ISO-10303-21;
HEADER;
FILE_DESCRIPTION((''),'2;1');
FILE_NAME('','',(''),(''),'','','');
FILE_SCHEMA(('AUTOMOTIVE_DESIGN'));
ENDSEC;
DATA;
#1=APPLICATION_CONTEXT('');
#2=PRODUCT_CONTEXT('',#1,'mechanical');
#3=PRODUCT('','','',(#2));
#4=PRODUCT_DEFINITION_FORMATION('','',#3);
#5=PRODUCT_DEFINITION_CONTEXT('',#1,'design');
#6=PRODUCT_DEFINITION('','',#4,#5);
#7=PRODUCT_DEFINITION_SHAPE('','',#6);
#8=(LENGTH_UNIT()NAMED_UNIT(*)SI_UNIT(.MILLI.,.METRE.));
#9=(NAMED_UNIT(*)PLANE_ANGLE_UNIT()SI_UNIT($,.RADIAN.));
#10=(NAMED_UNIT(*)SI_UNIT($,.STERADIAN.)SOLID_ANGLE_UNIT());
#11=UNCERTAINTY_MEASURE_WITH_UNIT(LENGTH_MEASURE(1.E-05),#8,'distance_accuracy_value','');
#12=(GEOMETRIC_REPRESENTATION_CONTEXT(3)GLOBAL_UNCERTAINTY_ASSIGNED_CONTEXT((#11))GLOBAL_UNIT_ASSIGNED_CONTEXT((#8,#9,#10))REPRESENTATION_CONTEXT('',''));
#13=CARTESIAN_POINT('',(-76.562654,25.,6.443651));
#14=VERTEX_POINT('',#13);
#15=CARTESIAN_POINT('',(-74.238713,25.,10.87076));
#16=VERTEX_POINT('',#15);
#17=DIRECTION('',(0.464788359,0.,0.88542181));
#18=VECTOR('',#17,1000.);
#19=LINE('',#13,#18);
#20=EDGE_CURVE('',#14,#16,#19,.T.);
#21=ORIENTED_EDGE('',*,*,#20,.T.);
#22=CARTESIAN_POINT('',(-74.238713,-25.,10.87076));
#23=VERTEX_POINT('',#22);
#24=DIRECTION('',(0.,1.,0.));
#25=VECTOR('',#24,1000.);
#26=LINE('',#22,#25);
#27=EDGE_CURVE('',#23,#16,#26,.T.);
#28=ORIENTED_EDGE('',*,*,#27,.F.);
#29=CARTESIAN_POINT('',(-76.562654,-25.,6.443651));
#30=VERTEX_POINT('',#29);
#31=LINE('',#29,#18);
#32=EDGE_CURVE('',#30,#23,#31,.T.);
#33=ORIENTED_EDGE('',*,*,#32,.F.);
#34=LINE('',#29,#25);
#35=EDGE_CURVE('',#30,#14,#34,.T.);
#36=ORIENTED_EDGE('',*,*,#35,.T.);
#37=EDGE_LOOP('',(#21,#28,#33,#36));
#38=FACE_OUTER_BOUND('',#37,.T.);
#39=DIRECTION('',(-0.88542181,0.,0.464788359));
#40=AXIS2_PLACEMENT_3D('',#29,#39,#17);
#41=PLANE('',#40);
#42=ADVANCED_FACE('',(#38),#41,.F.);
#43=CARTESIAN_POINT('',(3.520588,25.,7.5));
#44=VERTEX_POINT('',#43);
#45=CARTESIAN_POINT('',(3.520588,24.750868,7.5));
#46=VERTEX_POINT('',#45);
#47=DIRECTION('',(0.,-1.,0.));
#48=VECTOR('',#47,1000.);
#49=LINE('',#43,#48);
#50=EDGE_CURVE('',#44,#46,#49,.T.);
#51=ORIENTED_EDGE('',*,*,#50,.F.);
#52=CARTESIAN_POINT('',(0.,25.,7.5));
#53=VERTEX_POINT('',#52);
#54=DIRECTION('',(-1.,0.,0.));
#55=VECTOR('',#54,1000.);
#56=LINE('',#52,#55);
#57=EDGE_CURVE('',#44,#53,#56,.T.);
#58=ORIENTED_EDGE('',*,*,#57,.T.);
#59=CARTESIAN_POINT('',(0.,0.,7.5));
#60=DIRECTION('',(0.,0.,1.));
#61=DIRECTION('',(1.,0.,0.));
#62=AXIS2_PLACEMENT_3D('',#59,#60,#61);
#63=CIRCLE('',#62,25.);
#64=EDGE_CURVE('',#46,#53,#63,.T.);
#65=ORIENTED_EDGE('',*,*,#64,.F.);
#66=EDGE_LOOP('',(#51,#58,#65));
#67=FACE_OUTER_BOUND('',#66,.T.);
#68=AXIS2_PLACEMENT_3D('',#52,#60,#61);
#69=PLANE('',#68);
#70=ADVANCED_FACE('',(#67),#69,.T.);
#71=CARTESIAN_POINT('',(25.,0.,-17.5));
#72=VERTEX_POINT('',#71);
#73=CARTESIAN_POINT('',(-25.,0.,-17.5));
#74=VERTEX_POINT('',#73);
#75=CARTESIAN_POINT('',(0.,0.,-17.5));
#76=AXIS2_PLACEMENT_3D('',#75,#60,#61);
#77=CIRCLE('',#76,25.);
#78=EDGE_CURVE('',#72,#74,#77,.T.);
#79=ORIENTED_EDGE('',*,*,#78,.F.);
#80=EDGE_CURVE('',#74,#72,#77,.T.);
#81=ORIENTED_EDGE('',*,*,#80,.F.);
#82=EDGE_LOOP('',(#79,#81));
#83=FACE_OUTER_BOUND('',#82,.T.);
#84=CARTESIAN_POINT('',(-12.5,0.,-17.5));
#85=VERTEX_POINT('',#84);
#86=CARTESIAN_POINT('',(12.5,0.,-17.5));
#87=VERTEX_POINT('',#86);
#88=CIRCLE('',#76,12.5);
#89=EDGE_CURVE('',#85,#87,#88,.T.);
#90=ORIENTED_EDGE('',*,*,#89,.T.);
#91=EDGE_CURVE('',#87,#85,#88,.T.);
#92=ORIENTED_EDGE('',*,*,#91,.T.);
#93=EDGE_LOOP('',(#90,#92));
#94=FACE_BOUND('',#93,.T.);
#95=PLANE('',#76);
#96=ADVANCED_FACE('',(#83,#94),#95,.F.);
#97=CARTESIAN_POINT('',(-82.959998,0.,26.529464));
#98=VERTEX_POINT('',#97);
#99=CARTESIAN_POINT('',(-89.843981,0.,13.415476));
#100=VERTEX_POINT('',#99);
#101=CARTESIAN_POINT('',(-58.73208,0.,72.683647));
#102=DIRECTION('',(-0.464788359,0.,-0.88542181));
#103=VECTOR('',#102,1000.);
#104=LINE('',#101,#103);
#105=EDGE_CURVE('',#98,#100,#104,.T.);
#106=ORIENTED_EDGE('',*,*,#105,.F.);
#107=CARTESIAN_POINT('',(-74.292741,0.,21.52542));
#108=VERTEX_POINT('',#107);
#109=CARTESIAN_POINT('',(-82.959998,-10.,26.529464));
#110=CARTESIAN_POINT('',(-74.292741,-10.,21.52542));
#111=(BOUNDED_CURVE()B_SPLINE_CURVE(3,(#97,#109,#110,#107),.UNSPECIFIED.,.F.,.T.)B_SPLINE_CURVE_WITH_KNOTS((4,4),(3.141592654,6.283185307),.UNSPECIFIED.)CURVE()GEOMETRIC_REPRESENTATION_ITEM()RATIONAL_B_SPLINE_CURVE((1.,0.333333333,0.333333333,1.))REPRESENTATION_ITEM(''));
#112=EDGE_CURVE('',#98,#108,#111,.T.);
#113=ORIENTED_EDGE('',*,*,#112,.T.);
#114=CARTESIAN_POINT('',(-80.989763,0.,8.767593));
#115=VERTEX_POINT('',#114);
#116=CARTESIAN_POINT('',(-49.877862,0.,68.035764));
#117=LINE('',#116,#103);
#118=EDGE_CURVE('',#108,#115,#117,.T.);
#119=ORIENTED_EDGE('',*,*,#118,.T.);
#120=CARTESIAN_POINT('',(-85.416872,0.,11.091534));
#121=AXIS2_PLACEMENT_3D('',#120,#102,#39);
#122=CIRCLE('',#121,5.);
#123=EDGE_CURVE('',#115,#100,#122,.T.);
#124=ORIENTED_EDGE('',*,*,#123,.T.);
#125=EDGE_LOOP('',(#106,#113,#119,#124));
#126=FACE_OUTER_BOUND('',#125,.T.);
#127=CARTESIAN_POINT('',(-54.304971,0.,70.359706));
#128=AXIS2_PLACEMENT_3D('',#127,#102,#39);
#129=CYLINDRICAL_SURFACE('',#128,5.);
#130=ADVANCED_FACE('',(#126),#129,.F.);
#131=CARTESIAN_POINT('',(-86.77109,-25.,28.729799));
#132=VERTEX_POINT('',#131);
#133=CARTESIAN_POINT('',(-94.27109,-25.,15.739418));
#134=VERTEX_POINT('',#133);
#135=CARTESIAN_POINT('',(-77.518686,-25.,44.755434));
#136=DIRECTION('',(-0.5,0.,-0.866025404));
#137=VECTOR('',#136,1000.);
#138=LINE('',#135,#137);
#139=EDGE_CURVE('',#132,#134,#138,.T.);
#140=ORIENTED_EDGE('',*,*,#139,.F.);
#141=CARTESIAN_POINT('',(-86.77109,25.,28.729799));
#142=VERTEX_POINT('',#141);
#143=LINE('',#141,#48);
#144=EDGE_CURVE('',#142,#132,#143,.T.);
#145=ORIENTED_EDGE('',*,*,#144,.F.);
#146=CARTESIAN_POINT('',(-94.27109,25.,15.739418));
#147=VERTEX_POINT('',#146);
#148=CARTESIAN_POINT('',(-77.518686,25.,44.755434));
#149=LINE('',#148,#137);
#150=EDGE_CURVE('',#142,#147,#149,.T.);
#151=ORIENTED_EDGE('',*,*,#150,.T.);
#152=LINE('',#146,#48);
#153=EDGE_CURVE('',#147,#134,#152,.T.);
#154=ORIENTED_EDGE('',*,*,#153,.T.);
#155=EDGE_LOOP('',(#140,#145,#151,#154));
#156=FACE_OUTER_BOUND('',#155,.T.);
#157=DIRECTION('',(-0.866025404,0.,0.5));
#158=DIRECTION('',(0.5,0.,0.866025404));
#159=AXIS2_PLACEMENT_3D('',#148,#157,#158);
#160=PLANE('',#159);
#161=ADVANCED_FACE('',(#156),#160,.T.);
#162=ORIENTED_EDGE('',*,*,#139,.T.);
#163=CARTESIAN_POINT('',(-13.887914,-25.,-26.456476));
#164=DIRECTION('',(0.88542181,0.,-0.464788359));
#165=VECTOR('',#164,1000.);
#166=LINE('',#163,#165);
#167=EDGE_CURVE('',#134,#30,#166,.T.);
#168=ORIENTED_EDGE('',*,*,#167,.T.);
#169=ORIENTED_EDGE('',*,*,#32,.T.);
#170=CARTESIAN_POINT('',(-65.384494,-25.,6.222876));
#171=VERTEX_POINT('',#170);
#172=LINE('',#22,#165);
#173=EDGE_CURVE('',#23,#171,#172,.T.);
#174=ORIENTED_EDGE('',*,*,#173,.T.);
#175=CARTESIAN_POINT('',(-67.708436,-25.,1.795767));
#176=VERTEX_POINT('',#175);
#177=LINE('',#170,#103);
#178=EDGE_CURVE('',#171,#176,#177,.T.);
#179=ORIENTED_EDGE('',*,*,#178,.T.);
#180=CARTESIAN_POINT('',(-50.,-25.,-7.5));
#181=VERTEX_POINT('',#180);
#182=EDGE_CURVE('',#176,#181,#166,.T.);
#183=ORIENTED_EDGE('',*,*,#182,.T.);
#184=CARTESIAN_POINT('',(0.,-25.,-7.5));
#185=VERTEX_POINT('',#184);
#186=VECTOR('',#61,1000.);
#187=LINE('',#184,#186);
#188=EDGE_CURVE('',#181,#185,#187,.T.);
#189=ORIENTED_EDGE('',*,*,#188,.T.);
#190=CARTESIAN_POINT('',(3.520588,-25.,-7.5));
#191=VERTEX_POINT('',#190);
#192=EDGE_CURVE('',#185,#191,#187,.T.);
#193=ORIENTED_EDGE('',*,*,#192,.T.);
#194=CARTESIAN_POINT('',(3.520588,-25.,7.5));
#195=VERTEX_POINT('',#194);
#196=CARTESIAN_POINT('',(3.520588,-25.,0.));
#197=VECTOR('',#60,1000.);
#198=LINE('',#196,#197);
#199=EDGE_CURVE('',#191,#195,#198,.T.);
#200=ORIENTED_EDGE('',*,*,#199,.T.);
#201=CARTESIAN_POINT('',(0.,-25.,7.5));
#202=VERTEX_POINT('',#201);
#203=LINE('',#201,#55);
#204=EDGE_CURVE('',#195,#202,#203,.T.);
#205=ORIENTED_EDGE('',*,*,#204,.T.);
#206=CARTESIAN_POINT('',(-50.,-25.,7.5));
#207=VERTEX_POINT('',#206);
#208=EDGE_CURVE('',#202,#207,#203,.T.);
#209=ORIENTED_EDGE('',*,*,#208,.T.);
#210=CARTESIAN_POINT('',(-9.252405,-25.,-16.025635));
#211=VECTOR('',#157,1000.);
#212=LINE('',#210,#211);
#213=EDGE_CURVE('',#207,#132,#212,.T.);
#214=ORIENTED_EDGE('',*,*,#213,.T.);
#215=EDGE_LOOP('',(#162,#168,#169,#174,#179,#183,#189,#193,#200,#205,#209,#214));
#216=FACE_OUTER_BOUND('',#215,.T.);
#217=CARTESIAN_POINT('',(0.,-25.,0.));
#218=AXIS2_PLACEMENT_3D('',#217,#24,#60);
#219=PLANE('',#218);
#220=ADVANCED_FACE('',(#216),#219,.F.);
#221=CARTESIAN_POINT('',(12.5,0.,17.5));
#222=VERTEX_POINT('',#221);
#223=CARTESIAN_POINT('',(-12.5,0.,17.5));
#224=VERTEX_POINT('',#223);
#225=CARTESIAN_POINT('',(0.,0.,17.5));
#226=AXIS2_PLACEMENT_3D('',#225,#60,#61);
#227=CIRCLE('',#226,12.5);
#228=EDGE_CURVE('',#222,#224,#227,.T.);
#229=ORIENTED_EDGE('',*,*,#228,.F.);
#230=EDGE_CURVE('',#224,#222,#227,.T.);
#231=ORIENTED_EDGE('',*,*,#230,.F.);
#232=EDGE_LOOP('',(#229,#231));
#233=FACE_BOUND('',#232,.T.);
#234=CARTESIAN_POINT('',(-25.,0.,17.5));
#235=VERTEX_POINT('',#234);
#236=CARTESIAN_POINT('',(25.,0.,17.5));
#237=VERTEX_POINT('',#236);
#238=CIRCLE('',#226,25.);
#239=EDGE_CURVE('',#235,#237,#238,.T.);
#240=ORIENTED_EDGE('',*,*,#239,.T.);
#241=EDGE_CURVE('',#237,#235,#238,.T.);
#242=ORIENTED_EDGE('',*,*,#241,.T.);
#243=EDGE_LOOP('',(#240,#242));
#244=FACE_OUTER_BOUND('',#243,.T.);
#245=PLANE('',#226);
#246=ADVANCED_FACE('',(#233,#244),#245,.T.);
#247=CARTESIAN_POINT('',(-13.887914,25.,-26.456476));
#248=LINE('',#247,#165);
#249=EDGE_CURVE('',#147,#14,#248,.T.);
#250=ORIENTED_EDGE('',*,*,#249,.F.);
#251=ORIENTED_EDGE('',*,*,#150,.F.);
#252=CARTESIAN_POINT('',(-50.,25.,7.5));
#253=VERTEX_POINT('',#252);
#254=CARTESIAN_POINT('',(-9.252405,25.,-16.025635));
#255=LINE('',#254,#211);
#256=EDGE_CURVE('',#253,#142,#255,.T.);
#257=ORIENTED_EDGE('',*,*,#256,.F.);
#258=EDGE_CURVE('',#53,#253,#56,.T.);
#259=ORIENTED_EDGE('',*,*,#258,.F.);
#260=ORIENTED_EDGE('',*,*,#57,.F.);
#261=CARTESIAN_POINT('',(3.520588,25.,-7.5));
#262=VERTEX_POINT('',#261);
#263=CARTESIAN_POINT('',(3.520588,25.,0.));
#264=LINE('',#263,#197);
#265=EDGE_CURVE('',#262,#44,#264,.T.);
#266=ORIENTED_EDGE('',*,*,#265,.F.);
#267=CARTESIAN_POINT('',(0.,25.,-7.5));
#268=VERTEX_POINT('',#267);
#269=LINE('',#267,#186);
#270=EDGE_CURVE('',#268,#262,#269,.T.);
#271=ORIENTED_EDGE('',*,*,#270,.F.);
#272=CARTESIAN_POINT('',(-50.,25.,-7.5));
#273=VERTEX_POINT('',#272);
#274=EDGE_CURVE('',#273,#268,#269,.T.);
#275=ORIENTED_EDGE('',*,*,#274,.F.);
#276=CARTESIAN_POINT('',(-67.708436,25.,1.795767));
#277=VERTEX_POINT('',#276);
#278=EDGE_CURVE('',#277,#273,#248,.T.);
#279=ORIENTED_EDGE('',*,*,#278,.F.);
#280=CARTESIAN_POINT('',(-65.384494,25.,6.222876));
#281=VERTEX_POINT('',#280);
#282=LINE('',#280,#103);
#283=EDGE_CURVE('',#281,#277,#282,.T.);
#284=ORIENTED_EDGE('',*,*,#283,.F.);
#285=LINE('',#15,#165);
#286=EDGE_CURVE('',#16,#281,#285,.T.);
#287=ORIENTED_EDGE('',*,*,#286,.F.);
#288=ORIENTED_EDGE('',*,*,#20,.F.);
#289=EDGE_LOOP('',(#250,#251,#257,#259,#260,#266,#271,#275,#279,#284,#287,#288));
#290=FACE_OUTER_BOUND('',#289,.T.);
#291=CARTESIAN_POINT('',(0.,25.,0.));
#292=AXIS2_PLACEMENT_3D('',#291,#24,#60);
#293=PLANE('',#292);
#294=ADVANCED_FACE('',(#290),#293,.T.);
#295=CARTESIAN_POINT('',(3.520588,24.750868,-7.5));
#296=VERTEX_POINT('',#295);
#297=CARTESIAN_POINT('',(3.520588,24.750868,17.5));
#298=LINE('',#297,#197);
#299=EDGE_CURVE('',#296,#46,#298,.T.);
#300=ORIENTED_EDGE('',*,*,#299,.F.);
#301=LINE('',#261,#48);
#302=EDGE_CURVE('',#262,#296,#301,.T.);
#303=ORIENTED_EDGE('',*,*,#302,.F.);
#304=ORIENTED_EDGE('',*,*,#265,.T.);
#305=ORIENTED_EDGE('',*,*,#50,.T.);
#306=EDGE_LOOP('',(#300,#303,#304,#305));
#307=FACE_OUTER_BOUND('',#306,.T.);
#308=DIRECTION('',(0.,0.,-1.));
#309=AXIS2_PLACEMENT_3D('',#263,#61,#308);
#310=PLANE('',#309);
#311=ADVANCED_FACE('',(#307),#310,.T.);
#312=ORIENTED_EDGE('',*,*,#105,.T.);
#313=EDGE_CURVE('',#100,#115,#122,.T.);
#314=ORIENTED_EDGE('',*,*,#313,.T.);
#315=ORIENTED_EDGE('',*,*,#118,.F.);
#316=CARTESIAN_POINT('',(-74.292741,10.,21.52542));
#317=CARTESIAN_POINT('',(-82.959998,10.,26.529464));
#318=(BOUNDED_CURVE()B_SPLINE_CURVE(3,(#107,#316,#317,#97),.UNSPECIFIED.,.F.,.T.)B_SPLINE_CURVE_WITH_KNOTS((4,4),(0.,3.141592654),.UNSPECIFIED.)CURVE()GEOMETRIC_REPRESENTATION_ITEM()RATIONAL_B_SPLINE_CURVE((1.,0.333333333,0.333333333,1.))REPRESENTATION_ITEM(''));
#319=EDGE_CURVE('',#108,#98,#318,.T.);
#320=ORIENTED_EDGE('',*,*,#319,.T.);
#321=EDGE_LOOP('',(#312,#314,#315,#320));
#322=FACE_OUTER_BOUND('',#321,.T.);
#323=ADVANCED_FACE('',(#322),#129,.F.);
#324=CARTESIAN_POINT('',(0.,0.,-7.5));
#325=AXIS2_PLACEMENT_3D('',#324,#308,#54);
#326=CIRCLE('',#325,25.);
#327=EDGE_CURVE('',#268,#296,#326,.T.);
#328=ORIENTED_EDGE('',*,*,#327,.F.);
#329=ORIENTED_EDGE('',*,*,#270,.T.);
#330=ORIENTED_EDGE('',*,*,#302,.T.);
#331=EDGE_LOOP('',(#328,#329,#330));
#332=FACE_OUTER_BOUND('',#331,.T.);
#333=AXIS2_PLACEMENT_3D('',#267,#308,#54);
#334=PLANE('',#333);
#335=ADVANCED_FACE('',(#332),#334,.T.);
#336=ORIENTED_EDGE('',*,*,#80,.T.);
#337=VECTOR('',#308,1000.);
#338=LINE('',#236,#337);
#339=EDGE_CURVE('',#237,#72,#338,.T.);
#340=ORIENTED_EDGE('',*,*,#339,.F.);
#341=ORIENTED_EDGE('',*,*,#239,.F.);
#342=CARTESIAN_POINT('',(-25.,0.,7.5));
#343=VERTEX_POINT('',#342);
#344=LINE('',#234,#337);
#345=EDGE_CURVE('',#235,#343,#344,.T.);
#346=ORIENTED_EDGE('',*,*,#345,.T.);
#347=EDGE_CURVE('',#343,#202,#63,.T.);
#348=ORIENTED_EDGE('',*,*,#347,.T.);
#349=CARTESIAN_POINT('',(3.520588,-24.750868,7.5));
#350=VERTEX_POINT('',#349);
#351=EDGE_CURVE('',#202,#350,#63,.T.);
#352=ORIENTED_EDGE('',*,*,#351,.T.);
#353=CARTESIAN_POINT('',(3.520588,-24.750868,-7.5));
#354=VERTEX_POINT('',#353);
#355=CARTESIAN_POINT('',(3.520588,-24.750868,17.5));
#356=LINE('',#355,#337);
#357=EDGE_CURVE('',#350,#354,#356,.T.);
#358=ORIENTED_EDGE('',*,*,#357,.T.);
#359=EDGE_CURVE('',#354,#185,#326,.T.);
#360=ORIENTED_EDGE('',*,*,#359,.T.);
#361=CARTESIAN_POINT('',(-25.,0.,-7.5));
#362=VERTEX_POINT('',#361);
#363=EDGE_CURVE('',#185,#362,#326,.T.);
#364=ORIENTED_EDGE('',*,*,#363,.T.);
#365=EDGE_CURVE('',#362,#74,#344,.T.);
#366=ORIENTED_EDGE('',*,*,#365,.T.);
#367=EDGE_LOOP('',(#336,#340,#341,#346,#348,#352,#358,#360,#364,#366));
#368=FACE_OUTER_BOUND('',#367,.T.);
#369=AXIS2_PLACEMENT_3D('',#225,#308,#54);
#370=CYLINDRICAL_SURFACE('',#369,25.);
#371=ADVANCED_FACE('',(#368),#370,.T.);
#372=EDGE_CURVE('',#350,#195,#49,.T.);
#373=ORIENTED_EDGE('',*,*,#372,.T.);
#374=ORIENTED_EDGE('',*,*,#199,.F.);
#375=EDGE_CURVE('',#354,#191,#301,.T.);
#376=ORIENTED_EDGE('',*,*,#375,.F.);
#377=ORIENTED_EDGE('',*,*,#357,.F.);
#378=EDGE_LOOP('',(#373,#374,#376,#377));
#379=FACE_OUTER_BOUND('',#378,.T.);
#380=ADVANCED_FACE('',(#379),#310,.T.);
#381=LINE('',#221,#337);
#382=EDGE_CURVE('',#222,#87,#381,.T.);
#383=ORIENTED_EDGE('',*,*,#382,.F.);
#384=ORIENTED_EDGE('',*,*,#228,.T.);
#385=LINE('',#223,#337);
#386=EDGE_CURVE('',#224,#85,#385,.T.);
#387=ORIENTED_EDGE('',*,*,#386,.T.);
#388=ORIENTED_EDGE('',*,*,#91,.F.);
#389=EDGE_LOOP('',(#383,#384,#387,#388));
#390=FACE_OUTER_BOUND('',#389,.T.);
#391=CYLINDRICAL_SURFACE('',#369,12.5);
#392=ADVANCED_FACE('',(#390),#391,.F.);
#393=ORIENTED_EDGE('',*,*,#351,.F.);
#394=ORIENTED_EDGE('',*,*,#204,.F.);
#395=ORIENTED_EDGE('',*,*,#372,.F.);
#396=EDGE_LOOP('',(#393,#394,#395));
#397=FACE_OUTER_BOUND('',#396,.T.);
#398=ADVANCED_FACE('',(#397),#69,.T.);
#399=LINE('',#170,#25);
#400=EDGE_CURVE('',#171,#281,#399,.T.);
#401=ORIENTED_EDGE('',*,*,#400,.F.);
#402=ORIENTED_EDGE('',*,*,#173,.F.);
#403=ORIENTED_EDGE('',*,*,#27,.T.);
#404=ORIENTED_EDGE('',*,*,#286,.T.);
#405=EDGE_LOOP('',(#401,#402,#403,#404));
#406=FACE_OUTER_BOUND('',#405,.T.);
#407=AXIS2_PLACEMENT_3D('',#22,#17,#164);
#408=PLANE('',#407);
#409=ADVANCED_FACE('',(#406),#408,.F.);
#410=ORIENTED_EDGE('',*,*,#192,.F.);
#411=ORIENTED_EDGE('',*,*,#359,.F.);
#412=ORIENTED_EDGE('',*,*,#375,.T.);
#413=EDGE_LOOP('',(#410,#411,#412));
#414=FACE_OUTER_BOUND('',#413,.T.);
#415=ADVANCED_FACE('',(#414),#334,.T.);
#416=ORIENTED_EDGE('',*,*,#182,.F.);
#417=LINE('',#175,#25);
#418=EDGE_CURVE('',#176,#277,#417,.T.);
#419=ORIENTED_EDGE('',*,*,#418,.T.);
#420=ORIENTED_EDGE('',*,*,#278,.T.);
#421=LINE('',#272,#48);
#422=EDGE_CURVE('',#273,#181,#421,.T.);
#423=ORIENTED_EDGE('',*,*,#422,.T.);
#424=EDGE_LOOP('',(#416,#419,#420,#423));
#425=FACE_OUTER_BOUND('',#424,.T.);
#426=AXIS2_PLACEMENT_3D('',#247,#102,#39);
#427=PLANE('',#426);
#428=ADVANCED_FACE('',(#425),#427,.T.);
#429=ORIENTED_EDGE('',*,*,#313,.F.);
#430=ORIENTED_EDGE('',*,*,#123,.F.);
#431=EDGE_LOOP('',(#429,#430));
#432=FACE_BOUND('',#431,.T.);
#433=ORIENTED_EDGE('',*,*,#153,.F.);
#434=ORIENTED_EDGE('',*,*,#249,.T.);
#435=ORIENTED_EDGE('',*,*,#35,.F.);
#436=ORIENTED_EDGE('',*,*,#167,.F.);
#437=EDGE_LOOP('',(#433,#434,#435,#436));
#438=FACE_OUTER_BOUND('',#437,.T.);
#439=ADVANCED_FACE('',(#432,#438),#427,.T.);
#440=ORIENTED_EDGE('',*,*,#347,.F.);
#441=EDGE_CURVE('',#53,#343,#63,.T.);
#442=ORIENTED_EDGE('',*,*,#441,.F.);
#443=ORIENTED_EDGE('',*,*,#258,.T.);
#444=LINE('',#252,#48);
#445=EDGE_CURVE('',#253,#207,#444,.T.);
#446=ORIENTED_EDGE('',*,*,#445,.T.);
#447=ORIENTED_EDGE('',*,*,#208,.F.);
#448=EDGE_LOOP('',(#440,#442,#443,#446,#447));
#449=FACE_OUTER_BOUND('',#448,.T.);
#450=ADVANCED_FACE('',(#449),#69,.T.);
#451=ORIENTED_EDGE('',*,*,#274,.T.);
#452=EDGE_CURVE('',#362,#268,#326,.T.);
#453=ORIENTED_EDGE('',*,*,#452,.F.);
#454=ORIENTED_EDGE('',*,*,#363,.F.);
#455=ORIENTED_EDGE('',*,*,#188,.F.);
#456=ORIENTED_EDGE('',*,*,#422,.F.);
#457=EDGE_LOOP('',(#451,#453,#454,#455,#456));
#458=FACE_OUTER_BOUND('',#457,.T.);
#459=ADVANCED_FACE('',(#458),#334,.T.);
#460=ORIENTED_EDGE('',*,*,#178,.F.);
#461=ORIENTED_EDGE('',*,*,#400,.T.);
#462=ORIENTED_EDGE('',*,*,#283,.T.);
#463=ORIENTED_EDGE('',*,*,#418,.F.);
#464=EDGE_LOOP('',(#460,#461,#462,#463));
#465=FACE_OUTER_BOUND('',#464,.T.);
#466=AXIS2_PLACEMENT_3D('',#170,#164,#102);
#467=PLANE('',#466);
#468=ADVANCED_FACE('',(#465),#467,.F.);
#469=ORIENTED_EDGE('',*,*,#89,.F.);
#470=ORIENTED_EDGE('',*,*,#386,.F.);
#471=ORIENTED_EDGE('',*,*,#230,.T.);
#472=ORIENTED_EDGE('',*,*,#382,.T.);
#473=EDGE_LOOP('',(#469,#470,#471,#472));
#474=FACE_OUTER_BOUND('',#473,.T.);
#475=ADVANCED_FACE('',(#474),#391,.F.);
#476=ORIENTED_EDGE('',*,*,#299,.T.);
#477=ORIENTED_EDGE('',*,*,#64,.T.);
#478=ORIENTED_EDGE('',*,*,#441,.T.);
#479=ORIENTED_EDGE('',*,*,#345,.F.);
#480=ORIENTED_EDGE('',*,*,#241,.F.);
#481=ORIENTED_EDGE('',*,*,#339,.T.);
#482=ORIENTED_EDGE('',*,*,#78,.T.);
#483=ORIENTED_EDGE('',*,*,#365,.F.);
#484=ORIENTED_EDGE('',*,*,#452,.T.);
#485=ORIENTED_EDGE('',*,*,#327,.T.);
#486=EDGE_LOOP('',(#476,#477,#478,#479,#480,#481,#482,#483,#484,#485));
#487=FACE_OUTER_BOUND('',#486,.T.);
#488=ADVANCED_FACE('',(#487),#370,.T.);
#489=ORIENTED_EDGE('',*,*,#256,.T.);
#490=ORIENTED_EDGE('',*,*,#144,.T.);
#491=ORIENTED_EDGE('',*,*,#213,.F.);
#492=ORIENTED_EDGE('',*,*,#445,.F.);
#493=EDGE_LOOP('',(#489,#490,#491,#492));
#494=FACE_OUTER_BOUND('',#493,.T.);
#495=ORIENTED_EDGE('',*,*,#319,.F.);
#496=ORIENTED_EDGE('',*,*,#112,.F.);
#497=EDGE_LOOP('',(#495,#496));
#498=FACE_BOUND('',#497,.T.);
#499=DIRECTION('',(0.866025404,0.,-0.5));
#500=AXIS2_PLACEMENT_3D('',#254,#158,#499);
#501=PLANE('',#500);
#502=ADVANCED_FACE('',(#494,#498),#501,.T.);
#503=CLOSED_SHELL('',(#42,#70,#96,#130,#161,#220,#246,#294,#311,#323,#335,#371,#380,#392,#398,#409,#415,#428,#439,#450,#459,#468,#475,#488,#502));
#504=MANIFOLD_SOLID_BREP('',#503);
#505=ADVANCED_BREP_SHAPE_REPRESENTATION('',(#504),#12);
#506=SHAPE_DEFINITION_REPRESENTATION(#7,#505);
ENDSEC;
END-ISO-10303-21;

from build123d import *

# Parameters (mm, degrees)
HUB_TUBE_SKETCH_50_25_R   = 25
HUB_TUBE_SKETCH_50_25_R_2 = 12.5
HUB_TUBE_50_25_X35_DEPTH  = 17.5
ARM_50_DEPTH              = 25
TOP_NOTCH_CUT_DEPTH       = 111.509908397
CROSS_HOLE_SKETCH_10_R    = 5
CROSS_HOLE_10_DEPTH       = 101.657736852
BORE_CLEARANCE_CUT_DEPTH  = 108.931611768


with BuildPart() as part:
    # Hub Tube Sketch Ø50-Ø25 → Hub Tube Ø50-Ø25 x35 (new, symmetric)
    with BuildSketch(Plane.XY):
        Circle(HUB_TUBE_SKETCH_50_25_R)
        Circle(HUB_TUBE_SKETCH_50_25_R_2, mode=Mode.SUBTRACT)
    extrude(amount=HUB_TUBE_50_25_X35_DEPTH, both=True)

    # Arm Profile Sketch → Arm 50 (add, symmetric)
    with BuildSketch(Plane(origin=(0, 0, 0), x_dir=(1, 0, 0), z_dir=(0, 1, 0))):
        Polygon((3.520588359, 7.5), (-25, 7.5), (-50, 7.5), (-94.271090497, -15.73941794), (-86.771090497, -28.729798997), (-50, -7.5), (-25, -7.5), (3.520588359, -7.5), align=None)
    extrude(amount=ARM_50_DEPTH, both=True)

    # Top Notch Sketch → Top Notch Cut (cut, through all)
    with BuildSketch(Plane(origin=(0, 25, 0), x_dir=(1, 0, 0), z_dir=(0, 1, 0))):
        Polygon((-76.562654298, -6.443650764), (-74.238712504, -10.870759814), (-65.384494405, -6.222876226), (-67.708436199, -1.795767176), align=None)
    extrude(amount=-TOP_NOTCH_CUT_DEPTH, mode=Mode.SUBTRACT)

    # Cross Hole Sketch Ø10 → Cross Hole Ø10 (cut, through all)
    with BuildSketch(Plane(origin=(-13.887914048, 0, -26.456475856), x_dir=(-0.8854218099422658, 0, 0.46478835880275915), z_dir=(-0.46478835880275915, 0, -0.8854218099422658))):
        with Locations((80.785177806, 0)):
            Circle(CROSS_HOLE_SKETCH_10_R)
    extrude(amount=-CROSS_HOLE_10_DEPTH, mode=Mode.SUBTRACT)

    # Bore Clearance Sketch → Bore Clearance Cut (cut, through all)
    with BuildSketch(Plane(origin=(0, 0, -17.5), x_dir=(-1, 0, 0), z_dir=(0, 0, -1))):
        with BuildLine():
            Line((-3.520588359, 11.993975888), (-3.520588359, -11.993975888))
            ThreePointArc((-3.520588359, -11.993975888), (12.5, 0), (-3.520588359, 11.993975888))
        make_face()
    extrude(amount=-BORE_CLEARANCE_CUT_DEPTH, mode=Mode.SUBTRACT)


solid = part.part
